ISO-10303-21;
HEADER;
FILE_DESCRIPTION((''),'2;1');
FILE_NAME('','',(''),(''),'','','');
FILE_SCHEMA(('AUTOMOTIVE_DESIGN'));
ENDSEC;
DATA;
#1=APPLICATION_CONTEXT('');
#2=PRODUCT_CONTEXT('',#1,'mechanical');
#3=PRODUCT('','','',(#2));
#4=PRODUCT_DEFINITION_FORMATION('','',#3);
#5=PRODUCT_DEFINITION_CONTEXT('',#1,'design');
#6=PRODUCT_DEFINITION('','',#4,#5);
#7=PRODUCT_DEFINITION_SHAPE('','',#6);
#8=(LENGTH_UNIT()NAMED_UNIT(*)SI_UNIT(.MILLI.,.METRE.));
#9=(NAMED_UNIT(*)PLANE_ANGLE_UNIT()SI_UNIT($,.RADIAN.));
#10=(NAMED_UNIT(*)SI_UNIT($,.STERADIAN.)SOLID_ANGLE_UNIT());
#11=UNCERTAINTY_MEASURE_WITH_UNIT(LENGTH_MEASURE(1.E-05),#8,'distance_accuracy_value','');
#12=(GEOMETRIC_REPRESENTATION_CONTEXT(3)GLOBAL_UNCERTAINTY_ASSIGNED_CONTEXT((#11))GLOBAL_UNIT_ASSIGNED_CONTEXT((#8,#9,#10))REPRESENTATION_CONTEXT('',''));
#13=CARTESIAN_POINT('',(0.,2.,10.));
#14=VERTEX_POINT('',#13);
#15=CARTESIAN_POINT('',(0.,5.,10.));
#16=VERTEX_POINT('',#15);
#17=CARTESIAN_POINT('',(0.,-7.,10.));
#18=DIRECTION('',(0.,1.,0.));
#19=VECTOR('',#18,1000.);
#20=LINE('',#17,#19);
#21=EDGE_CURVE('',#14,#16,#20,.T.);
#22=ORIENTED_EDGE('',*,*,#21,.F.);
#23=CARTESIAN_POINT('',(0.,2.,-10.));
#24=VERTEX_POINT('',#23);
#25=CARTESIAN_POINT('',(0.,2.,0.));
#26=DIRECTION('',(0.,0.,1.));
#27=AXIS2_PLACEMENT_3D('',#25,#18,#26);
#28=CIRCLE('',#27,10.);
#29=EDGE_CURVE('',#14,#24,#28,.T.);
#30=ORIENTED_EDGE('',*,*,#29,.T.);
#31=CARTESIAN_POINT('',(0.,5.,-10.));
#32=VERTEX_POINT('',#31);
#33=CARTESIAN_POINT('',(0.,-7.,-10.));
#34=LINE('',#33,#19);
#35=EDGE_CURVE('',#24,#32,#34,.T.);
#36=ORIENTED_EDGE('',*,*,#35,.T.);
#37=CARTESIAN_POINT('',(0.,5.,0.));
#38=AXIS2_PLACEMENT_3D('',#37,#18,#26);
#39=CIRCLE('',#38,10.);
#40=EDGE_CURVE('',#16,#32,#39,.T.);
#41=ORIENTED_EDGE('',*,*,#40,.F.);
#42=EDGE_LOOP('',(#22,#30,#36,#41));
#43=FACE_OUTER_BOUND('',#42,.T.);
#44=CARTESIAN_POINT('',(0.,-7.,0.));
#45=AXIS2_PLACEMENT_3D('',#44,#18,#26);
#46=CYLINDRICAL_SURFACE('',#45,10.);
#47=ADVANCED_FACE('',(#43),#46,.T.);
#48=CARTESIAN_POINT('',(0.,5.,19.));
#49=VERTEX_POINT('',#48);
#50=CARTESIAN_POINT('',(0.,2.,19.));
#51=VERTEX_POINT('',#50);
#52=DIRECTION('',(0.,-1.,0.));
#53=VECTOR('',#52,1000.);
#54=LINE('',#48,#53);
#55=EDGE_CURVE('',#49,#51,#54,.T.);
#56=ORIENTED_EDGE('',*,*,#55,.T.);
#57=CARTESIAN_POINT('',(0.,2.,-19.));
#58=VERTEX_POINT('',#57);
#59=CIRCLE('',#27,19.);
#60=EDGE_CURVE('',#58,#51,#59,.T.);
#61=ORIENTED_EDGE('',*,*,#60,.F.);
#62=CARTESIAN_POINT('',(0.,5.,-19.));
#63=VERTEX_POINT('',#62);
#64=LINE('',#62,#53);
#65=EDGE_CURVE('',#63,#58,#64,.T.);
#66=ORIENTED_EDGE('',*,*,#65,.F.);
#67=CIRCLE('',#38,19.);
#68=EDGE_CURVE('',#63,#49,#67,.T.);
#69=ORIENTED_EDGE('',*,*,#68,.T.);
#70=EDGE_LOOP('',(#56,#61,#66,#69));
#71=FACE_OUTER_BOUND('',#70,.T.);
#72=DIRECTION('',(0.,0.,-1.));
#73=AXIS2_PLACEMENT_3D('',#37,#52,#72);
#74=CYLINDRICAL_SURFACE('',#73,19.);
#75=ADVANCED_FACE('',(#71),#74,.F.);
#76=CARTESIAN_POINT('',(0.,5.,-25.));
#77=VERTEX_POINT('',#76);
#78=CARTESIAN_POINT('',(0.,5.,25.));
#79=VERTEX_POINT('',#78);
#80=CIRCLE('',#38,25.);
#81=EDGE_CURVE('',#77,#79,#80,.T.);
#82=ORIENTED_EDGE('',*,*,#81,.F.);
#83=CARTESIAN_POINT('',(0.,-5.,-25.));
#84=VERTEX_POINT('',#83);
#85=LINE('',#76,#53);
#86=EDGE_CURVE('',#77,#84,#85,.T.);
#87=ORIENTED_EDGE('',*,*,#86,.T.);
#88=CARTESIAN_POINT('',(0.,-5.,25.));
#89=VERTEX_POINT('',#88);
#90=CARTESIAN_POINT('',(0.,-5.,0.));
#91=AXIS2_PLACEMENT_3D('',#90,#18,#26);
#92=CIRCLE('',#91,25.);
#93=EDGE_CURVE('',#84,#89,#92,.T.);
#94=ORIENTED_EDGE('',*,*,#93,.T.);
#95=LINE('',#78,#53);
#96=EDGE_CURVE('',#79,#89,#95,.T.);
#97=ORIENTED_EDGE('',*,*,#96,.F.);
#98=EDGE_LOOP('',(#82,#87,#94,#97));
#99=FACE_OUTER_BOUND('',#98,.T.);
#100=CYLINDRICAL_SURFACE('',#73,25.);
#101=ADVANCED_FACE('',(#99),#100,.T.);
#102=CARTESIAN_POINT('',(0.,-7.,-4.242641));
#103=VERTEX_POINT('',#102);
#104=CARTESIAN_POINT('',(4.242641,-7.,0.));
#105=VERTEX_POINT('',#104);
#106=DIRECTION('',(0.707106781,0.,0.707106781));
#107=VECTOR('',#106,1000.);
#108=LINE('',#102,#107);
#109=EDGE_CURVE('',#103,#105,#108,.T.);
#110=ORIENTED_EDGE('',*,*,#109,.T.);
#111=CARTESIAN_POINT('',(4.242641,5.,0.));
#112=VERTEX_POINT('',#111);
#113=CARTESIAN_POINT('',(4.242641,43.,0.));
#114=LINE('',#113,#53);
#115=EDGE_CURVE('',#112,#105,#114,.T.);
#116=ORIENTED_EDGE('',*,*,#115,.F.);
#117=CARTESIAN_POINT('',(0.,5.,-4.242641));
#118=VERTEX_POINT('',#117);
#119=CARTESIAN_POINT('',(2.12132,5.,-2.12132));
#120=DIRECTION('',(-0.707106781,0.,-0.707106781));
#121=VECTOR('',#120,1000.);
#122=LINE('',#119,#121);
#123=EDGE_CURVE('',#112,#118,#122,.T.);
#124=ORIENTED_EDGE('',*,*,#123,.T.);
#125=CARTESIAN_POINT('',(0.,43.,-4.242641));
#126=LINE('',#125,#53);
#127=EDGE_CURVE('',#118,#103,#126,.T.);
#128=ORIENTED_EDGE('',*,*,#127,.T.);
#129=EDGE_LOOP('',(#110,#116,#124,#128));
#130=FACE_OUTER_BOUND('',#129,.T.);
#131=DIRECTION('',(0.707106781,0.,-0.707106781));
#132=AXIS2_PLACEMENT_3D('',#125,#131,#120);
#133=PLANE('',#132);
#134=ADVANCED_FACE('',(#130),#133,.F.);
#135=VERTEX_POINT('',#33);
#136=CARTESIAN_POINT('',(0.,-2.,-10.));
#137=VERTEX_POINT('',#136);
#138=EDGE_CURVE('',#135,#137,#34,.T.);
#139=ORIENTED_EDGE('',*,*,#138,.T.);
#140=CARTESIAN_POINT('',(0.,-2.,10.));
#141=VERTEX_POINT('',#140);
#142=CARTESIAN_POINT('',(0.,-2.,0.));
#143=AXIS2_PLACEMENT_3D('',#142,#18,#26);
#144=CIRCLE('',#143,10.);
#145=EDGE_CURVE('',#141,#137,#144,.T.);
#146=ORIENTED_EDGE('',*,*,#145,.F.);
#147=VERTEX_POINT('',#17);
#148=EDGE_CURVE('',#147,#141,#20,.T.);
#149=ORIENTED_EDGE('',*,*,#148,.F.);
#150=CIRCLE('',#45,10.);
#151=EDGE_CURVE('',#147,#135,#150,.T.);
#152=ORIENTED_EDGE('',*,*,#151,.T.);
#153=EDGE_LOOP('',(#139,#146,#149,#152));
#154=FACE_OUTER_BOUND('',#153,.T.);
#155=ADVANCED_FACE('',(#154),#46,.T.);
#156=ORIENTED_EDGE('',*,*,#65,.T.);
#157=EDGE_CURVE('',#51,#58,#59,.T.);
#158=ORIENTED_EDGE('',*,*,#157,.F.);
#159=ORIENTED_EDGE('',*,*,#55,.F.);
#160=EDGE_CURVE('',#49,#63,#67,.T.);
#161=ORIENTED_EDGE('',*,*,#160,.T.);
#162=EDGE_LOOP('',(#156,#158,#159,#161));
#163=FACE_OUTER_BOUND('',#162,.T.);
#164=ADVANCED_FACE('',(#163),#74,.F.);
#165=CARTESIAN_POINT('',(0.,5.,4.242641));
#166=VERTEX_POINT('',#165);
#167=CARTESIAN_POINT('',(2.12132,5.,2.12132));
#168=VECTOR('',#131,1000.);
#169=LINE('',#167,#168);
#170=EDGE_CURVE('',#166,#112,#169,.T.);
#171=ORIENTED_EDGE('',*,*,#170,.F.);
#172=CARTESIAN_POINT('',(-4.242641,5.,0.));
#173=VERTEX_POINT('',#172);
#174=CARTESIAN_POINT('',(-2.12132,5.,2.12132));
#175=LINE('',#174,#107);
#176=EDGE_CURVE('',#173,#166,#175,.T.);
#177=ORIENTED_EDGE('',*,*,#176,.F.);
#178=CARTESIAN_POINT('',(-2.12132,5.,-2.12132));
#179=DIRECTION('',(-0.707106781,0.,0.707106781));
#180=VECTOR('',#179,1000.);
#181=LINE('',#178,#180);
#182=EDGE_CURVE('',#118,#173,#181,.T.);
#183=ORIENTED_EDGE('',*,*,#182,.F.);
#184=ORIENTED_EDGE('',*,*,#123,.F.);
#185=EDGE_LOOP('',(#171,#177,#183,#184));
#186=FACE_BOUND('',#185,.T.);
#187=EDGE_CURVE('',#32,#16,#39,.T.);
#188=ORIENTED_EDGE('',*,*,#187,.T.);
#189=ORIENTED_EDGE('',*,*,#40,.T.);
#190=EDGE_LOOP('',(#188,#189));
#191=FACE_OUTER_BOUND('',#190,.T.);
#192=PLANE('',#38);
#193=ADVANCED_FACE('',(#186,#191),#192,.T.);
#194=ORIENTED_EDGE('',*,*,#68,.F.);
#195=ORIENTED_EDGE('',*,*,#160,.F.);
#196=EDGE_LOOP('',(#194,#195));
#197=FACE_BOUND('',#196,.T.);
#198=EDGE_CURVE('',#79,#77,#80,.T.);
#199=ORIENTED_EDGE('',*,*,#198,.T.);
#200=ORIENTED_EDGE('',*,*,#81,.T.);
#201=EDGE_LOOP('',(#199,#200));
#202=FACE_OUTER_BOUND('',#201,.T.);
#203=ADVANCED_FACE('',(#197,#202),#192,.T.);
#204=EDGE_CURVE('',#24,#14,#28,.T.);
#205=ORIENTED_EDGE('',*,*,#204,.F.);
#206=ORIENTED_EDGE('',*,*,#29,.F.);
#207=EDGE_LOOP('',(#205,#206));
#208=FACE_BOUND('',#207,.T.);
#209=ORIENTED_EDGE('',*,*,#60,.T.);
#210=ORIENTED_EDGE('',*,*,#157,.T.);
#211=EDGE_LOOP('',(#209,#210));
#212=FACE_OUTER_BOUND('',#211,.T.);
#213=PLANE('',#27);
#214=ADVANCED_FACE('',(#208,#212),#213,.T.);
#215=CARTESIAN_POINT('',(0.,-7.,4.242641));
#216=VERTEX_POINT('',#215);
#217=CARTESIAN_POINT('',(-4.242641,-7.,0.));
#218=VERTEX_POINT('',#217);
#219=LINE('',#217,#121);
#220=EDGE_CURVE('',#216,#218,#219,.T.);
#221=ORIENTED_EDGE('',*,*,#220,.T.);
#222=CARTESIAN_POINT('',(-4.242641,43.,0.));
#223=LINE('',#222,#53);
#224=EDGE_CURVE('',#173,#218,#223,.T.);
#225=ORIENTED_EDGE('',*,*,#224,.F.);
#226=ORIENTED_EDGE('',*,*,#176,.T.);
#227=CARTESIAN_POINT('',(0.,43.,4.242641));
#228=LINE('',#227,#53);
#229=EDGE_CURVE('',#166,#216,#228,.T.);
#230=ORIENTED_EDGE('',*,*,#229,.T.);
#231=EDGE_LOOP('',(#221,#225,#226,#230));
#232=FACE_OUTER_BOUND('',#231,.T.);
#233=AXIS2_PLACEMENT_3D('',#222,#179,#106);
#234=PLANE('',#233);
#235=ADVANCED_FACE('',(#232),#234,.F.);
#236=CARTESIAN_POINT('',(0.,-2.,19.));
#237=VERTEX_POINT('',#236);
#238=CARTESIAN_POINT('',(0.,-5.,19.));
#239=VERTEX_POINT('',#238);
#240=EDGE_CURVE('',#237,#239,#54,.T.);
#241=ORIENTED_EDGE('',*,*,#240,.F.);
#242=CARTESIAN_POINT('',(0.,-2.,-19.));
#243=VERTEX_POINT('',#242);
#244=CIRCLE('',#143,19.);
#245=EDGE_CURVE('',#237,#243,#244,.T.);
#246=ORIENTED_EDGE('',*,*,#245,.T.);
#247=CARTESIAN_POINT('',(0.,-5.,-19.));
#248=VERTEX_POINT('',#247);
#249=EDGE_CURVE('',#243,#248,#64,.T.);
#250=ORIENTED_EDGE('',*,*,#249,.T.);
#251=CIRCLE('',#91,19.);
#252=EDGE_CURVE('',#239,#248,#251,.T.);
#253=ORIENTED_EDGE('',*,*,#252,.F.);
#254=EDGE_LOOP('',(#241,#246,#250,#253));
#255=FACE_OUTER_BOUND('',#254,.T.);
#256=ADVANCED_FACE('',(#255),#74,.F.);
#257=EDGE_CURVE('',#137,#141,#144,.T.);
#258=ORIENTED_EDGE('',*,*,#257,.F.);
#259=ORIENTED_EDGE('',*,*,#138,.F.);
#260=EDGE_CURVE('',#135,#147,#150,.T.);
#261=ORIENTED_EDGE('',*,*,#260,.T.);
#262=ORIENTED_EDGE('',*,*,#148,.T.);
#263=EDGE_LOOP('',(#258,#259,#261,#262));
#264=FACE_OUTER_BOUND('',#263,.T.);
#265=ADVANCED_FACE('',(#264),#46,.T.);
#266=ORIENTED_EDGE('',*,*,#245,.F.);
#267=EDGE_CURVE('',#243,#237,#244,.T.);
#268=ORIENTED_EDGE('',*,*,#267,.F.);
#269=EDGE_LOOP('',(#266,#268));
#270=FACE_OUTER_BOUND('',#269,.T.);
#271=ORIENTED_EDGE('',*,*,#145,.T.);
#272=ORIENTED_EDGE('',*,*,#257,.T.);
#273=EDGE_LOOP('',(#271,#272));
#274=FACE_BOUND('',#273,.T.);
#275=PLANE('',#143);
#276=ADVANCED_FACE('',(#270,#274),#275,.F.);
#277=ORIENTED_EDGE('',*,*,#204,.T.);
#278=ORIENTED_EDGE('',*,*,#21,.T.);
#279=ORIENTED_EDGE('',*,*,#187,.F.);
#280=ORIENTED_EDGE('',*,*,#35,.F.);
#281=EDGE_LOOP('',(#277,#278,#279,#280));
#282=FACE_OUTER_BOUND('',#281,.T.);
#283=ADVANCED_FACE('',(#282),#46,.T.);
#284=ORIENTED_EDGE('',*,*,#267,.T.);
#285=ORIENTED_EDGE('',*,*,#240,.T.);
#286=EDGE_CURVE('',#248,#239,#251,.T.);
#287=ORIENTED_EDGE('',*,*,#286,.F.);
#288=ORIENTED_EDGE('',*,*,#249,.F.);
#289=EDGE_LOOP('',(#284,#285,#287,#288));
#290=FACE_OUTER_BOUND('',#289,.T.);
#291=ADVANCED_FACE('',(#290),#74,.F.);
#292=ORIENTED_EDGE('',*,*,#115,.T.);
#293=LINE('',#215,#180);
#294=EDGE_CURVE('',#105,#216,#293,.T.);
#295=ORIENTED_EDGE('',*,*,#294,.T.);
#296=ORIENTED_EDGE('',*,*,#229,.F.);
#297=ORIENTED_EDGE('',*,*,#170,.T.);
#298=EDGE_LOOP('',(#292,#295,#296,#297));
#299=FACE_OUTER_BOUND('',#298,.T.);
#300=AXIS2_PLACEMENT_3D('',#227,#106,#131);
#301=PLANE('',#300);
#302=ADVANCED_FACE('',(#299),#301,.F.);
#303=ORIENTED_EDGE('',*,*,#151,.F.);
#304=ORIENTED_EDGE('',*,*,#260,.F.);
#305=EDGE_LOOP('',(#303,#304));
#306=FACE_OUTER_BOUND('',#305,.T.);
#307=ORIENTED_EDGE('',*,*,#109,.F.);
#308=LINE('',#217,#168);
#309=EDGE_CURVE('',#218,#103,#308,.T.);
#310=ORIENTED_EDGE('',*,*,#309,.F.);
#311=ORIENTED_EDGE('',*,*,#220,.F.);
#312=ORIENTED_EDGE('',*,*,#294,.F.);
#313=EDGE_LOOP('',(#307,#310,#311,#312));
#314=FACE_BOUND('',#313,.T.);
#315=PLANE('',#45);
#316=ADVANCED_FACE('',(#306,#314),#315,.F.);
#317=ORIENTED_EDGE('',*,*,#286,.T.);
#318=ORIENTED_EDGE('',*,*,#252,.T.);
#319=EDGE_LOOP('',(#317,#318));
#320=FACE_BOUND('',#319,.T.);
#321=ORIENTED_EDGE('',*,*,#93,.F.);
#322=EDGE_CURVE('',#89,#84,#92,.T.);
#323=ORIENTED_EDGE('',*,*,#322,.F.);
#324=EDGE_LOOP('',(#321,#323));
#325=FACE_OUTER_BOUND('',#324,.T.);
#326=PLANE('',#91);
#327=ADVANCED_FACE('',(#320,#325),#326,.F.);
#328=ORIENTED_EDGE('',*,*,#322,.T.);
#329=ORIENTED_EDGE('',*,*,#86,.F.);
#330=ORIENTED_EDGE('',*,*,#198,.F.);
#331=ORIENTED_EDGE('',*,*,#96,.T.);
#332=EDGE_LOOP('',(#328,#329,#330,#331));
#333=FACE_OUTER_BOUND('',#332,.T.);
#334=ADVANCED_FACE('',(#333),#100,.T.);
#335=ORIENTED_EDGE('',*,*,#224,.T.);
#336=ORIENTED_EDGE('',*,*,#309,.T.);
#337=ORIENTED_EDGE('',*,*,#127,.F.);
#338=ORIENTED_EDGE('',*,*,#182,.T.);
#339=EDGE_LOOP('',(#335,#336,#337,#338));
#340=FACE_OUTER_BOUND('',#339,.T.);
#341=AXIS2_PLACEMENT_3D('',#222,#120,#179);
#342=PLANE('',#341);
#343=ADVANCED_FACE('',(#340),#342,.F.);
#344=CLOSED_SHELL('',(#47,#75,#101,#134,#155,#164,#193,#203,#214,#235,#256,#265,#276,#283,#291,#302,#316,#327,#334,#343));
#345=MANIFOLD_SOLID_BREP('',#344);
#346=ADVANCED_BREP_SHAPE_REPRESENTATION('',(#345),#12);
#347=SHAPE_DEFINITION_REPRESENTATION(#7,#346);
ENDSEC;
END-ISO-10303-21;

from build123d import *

# Parameters (mm, degrees)
SKETCH1_R           = 25
SKETCH1_R_2         = 19
BOSS_EXTRUDE1_DEPTH = 5
SKETCH2_R           = 10
BOSS_EXTRUDE2_DEPTH = 12
SKETCH3_R           = 19
SKETCH3_R_2         = 10
BOSS_EXTRUDE3_DEPTH = 2
CUT_EXTRUDE1_DEPTH  = 50


with BuildPart() as part:
    # Sketch1 → Boss-Extrude1 (new, symmetric)
    with BuildSketch(Plane(origin=(0, 0, 0), x_dir=(1, 0, 0), z_dir=(0, 1, 0))):
        with Locations(Location((0, 0, 0), (0, 0, 270))):
            Circle(SKETCH1_R)
        with Locations(Location((0, 0, 0), (0, 0, 270))):
            Circle(SKETCH1_R_2, mode=Mode.SUBTRACT)
    extrude(amount=BOSS_EXTRUDE1_DEPTH, both=True)



with BuildPart() as body_2:
    # Sketch2 → Boss-Extrude2 (new body)
    with BuildSketch(Plane(origin=(0, 5, 0), x_dir=(1, 0, 0), z_dir=(0, 1, 0))):
        with Locations(Location((0, 0, 0), (0, 0, 270))):
            Circle(SKETCH2_R)
    extrude(amount=-BOSS_EXTRUDE2_DEPTH)


with BuildPart() as part_1:
    add(part.part)

    add(body_2.part)  # Boss-Extrude3 merges body 2
    # Sketch3 → Boss-Extrude3 (add, symmetric)
    with BuildSketch(Plane(origin=(0, 0, 0), x_dir=(1, 0, 0), z_dir=(0, 1, 0))):
        with Locations(Location((0, 0, 0), (0, 0, 270))):
            Circle(SKETCH3_R)
        with Locations(Location((0, 0, 0), (0, 0, 270))):
            Circle(SKETCH3_R_2, mode=Mode.SUBTRACT)
    extrude(amount=BOSS_EXTRUDE3_DEPTH, both=True)

    # Sketch4 → Cut-Extrude1 (cut)
    with BuildSketch(Plane.XZ.offset(7)):
        Polygon((-4.242640687, 0), (0, 4.242640687), (4.242640687, 0), (0, -4.242640687), align=None)
    extrude(amount=-CUT_EXTRUDE1_DEPTH, mode=Mode.SUBTRACT)


solid = part_1.part
